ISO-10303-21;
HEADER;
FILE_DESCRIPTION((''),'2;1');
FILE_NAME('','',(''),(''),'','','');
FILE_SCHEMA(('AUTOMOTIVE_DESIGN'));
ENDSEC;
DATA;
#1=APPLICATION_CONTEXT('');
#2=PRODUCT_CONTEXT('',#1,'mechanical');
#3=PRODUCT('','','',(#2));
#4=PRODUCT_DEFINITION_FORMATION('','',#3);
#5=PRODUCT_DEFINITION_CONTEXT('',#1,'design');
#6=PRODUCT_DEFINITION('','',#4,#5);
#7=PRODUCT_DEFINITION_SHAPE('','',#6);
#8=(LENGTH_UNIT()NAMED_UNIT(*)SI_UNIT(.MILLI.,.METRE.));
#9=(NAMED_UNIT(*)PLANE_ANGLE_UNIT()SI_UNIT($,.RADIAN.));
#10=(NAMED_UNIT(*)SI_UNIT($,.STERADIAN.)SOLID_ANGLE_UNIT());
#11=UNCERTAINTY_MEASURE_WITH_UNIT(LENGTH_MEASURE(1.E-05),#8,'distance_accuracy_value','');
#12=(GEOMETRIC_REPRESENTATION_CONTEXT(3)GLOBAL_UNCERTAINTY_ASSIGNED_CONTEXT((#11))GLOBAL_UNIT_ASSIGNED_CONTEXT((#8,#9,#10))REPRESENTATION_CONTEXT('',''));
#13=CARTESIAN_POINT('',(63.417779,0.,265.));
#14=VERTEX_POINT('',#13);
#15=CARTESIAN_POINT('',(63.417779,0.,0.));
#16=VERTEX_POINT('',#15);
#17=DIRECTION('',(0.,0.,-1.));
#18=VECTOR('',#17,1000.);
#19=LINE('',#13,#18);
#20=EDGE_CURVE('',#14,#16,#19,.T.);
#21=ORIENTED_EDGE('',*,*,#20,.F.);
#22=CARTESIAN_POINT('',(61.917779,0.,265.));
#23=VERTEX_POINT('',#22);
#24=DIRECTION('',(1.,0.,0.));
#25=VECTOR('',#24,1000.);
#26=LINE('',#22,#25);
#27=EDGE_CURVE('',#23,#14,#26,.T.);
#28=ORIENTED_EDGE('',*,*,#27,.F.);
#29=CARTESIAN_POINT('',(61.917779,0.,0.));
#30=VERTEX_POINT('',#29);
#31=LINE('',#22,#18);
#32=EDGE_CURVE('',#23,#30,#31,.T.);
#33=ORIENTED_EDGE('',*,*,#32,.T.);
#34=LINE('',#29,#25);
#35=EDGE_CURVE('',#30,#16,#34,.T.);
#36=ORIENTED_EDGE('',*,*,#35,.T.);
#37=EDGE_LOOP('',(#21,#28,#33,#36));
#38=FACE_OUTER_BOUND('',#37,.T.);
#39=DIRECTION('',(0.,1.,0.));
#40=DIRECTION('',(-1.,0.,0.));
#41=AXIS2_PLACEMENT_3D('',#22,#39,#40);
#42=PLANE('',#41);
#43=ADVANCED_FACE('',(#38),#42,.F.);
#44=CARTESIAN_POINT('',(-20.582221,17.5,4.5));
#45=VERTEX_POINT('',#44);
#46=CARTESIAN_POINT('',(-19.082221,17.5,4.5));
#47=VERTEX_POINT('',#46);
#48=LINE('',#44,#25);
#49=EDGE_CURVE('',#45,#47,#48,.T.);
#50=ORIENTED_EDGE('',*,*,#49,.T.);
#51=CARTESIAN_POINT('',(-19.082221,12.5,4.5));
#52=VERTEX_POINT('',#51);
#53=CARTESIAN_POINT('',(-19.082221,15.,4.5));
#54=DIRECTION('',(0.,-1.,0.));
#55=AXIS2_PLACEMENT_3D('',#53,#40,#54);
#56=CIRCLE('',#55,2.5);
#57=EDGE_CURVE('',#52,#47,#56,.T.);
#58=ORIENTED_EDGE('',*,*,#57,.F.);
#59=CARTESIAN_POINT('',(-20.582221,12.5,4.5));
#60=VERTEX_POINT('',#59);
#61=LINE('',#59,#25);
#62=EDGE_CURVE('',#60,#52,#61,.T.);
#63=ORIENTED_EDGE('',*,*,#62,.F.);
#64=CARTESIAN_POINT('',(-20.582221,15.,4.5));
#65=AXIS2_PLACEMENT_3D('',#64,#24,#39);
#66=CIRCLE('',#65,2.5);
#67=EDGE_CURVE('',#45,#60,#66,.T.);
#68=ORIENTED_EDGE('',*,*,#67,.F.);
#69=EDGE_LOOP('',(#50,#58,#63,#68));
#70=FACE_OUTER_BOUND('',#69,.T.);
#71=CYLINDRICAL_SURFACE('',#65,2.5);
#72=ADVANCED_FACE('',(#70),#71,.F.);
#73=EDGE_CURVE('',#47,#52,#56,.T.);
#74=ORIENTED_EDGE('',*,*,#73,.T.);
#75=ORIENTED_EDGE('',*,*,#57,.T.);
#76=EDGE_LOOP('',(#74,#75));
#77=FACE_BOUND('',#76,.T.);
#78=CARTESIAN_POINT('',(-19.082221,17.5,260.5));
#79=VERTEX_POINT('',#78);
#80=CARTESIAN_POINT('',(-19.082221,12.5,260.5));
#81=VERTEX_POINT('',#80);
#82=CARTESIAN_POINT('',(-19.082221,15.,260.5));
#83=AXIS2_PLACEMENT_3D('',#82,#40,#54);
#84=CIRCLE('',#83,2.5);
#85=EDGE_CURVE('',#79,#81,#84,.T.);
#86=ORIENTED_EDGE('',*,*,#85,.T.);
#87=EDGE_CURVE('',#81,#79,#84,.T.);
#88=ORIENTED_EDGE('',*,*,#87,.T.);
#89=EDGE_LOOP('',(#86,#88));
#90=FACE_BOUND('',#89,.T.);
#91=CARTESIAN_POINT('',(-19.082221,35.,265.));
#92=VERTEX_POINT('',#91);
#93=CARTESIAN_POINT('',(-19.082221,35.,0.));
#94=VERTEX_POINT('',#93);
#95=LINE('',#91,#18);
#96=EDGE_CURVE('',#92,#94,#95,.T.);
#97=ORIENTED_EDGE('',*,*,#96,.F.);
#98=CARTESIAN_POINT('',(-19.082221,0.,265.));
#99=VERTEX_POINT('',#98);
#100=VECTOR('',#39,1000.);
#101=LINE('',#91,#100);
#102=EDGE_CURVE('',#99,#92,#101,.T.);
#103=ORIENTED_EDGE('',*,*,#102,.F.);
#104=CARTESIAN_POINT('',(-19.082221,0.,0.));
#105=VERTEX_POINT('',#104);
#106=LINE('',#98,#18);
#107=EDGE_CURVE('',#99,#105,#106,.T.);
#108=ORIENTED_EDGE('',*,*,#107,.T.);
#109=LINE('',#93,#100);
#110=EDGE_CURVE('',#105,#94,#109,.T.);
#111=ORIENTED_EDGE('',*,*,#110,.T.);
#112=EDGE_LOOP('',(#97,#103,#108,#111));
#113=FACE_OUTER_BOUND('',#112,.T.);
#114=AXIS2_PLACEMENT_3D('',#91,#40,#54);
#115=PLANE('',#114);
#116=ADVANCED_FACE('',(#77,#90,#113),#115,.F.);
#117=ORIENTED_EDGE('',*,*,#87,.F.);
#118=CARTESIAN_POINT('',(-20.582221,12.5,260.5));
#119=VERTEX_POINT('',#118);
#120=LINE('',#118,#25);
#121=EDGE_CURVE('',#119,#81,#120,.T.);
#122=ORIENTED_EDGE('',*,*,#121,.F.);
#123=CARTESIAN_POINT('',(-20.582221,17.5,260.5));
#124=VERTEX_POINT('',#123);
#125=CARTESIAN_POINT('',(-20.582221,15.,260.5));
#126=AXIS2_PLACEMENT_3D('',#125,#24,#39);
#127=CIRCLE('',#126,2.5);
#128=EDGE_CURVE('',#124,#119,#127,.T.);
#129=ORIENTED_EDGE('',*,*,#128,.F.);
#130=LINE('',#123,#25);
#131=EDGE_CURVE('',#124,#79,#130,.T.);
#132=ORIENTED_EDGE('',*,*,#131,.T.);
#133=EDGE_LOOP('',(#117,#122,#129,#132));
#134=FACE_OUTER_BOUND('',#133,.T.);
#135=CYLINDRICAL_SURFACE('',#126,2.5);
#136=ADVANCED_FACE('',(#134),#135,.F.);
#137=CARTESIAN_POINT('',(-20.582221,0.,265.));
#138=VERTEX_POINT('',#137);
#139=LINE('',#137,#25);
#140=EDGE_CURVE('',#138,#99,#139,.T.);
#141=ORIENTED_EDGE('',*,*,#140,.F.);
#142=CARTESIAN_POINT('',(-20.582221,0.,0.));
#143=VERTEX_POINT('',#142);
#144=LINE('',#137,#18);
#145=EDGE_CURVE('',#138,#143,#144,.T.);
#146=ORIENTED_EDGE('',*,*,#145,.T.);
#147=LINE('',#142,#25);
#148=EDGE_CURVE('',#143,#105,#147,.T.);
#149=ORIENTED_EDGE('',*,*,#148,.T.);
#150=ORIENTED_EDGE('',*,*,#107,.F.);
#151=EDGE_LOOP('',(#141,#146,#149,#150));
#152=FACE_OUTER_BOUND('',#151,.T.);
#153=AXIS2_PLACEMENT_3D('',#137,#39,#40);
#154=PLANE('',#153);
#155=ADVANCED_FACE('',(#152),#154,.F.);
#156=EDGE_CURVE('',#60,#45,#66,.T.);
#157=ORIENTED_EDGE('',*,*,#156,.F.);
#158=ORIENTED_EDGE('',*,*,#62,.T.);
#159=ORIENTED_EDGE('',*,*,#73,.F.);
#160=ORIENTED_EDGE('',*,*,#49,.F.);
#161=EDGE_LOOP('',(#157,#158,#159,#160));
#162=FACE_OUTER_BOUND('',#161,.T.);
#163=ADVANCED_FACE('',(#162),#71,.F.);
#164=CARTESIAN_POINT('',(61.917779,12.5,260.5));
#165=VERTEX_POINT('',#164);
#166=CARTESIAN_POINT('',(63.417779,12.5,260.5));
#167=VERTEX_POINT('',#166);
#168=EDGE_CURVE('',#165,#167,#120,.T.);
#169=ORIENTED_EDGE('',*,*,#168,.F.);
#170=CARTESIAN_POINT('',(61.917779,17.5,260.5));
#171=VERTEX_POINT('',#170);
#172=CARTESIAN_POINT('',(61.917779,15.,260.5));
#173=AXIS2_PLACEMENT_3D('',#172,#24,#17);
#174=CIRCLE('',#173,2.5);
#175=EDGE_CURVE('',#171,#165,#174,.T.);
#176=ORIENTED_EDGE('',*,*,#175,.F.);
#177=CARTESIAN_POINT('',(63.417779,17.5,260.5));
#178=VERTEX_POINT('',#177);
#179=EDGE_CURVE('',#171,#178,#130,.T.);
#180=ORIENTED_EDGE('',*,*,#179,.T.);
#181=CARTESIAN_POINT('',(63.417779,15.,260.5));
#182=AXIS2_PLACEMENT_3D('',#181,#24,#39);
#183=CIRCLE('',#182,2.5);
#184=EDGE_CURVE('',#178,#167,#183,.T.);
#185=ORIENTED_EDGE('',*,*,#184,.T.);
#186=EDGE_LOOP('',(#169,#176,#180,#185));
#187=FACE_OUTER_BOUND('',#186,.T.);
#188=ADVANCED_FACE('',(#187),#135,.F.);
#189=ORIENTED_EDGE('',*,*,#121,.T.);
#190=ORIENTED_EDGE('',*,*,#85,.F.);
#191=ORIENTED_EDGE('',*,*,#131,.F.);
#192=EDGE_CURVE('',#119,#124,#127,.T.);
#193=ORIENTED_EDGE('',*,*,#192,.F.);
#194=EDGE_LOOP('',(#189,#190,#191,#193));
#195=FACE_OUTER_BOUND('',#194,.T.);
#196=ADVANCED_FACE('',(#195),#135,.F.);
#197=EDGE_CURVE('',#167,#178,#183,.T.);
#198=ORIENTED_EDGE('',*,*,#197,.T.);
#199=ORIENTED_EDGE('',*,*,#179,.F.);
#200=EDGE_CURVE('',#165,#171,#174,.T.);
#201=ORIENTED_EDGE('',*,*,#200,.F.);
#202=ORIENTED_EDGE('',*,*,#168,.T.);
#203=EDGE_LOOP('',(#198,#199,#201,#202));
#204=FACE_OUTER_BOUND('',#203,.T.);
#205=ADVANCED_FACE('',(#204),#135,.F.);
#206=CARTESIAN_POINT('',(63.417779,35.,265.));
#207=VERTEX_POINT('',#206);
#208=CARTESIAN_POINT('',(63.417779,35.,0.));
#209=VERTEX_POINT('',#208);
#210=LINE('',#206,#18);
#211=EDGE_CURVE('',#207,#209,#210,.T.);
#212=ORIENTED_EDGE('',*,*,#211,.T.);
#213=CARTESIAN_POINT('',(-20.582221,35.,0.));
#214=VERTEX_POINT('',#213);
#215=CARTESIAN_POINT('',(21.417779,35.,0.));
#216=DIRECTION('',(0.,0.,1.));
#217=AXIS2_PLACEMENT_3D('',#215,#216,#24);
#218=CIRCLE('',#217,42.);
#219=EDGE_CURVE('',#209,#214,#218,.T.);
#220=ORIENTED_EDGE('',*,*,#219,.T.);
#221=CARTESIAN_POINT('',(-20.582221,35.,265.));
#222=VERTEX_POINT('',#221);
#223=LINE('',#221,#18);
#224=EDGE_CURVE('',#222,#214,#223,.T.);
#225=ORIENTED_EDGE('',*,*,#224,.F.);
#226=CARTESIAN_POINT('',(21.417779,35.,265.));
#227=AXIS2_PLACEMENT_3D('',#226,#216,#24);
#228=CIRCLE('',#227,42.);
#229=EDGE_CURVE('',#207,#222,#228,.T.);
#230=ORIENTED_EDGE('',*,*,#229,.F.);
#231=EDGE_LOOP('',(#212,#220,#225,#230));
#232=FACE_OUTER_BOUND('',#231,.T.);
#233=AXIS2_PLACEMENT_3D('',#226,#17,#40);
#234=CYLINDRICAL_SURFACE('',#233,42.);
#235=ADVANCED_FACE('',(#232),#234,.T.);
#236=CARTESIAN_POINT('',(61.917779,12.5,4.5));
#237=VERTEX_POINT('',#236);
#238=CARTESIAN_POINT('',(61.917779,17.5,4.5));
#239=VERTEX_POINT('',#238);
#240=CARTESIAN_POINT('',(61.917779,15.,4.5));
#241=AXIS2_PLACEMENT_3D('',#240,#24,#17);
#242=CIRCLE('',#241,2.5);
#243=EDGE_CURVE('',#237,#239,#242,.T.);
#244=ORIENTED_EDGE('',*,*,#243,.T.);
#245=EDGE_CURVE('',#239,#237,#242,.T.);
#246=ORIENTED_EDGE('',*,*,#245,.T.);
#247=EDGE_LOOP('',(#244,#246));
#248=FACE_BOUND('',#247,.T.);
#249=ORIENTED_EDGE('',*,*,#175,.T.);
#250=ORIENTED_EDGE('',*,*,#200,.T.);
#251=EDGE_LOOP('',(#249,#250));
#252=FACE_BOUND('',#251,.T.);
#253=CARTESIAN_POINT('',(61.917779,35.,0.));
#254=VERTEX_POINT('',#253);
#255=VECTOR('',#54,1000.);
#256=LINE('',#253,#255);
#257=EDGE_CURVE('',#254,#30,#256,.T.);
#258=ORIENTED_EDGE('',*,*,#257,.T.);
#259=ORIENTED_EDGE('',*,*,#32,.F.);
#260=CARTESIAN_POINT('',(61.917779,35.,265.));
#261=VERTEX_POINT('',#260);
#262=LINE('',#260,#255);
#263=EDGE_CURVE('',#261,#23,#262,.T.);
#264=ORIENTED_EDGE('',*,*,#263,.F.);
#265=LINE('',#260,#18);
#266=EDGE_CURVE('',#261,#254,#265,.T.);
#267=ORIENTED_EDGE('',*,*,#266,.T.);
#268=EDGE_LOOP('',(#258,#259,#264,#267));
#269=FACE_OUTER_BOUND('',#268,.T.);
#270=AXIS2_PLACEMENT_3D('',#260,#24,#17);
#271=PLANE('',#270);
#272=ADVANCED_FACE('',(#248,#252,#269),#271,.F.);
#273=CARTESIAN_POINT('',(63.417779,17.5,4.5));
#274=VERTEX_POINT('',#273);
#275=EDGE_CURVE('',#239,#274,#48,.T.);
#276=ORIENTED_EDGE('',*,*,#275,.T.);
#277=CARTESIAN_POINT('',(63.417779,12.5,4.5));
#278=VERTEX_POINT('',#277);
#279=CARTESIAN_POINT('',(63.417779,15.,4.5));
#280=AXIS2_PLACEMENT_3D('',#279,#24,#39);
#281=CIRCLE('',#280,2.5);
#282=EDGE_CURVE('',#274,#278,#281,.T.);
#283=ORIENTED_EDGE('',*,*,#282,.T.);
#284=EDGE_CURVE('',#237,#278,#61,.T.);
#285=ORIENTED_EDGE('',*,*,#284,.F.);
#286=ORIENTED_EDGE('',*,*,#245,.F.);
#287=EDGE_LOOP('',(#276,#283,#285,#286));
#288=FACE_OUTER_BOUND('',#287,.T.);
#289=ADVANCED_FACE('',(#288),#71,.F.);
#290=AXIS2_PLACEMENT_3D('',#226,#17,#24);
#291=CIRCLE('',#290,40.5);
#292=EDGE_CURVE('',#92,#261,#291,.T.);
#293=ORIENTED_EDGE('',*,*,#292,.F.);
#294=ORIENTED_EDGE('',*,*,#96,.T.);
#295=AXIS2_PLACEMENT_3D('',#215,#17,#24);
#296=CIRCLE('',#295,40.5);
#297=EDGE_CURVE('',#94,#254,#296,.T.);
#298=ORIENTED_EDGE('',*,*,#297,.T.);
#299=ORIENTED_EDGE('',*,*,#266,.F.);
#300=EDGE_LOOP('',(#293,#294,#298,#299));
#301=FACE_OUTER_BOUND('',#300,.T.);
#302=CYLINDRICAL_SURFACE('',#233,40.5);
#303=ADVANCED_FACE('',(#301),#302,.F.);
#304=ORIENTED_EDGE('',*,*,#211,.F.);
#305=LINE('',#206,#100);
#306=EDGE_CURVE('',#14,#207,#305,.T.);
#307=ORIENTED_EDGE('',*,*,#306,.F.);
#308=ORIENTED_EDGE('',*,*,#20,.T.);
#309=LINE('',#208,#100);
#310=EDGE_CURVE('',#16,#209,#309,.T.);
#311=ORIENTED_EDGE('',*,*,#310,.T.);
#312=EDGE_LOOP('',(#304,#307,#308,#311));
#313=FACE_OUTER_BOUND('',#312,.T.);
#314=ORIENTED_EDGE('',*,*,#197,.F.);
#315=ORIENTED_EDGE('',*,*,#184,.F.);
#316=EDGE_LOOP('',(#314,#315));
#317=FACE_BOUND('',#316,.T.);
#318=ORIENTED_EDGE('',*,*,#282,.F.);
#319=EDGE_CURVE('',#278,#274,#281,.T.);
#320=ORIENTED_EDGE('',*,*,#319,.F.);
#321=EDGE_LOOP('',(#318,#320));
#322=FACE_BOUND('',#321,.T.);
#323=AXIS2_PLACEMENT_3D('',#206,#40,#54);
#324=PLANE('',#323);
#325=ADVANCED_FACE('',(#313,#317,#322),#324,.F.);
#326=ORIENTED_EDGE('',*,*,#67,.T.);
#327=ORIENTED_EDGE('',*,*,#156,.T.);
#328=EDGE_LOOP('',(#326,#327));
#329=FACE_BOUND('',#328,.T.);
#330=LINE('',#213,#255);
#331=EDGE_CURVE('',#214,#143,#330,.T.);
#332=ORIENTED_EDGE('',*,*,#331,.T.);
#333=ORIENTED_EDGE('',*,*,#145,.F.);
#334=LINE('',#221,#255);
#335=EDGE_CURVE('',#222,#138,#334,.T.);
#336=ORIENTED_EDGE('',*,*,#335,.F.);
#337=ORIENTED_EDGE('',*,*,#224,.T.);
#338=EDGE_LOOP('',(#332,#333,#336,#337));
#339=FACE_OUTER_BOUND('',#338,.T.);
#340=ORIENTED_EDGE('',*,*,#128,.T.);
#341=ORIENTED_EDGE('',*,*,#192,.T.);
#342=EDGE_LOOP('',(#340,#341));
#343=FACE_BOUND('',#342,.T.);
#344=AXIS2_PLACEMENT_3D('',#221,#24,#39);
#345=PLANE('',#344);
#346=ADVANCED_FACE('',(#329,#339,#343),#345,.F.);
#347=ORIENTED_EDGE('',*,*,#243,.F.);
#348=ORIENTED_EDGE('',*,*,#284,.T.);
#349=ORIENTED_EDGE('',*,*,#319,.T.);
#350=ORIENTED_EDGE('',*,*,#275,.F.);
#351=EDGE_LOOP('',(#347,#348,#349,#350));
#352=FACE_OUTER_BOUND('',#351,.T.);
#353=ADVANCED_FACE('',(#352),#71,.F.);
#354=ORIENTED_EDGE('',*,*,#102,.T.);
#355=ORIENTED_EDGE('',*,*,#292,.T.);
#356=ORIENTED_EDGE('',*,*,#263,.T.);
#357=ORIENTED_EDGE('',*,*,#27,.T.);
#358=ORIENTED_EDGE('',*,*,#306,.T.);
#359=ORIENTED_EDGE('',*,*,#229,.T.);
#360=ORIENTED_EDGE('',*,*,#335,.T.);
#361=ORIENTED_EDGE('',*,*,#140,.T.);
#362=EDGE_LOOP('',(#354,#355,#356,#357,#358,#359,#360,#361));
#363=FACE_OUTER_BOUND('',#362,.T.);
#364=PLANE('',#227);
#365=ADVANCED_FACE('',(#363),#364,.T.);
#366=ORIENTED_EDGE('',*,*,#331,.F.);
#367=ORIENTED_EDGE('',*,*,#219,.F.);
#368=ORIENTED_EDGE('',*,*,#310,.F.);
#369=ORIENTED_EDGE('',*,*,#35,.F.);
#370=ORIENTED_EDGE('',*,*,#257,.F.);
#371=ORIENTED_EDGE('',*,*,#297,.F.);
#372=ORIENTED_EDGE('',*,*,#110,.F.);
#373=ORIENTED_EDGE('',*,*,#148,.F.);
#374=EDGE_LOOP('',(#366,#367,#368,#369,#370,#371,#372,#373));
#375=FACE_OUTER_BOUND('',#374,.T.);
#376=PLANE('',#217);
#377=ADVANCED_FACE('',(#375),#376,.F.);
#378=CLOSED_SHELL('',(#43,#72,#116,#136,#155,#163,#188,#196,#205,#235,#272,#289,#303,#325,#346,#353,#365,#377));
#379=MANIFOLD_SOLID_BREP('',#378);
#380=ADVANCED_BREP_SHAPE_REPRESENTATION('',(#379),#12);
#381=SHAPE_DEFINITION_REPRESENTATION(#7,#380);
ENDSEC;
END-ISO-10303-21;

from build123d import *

# Parameters (mm, degrees)
EXTRUDE_1_DEPTH     = 265
SKETCH_2_R          = 2.5
CUT_EXTRUDE_1_DEPTH = 289.461435897


with BuildPart() as part:
    # 草图1 → 凸台-拉伸1 (new body)
    with BuildSketch(Plane.XY):
        with BuildLine():
            Line((-20.582221357, 0), (-19.082221357, 0))
            Line((-19.082221357, 0), (-19.082221357, 35))
            ThreePointArc((-19.082221357, 35), (21.417778643, 75.5), (61.917778643, 35))
            Line((61.917778643, 35), (61.917778643, 0))
            Line((61.917778643, 0), (63.417778643, 0))
            Line((63.417778643, 0), (63.417778643, 35))
            ThreePointArc((63.417778643, 35), (21.417778643, 77), (-20.582221357, 35))
            Line((-20.582221357, 35), (-20.582221357, 0))
        make_face()
    extrude(amount=EXTRUDE_1_DEPTH)

    # 草图2 → 切除-拉伸1 (cut, through all)
    with BuildSketch(Plane(origin=(63.417778643, 0, 0), x_dir=(0, 0, -1), z_dir=(1, 0, 0))):
        with Locations(Location((-260.5, 15, 0), (0, 0, 90))):
            Circle(SKETCH_2_R)
        with Locations(Location((-4.5, 15, 0), (0, 0, 90))):
            Circle(SKETCH_2_R)
    extrude(amount=-CUT_EXTRUDE_1_DEPTH, mode=Mode.SUBTRACT)


solid = part.part
